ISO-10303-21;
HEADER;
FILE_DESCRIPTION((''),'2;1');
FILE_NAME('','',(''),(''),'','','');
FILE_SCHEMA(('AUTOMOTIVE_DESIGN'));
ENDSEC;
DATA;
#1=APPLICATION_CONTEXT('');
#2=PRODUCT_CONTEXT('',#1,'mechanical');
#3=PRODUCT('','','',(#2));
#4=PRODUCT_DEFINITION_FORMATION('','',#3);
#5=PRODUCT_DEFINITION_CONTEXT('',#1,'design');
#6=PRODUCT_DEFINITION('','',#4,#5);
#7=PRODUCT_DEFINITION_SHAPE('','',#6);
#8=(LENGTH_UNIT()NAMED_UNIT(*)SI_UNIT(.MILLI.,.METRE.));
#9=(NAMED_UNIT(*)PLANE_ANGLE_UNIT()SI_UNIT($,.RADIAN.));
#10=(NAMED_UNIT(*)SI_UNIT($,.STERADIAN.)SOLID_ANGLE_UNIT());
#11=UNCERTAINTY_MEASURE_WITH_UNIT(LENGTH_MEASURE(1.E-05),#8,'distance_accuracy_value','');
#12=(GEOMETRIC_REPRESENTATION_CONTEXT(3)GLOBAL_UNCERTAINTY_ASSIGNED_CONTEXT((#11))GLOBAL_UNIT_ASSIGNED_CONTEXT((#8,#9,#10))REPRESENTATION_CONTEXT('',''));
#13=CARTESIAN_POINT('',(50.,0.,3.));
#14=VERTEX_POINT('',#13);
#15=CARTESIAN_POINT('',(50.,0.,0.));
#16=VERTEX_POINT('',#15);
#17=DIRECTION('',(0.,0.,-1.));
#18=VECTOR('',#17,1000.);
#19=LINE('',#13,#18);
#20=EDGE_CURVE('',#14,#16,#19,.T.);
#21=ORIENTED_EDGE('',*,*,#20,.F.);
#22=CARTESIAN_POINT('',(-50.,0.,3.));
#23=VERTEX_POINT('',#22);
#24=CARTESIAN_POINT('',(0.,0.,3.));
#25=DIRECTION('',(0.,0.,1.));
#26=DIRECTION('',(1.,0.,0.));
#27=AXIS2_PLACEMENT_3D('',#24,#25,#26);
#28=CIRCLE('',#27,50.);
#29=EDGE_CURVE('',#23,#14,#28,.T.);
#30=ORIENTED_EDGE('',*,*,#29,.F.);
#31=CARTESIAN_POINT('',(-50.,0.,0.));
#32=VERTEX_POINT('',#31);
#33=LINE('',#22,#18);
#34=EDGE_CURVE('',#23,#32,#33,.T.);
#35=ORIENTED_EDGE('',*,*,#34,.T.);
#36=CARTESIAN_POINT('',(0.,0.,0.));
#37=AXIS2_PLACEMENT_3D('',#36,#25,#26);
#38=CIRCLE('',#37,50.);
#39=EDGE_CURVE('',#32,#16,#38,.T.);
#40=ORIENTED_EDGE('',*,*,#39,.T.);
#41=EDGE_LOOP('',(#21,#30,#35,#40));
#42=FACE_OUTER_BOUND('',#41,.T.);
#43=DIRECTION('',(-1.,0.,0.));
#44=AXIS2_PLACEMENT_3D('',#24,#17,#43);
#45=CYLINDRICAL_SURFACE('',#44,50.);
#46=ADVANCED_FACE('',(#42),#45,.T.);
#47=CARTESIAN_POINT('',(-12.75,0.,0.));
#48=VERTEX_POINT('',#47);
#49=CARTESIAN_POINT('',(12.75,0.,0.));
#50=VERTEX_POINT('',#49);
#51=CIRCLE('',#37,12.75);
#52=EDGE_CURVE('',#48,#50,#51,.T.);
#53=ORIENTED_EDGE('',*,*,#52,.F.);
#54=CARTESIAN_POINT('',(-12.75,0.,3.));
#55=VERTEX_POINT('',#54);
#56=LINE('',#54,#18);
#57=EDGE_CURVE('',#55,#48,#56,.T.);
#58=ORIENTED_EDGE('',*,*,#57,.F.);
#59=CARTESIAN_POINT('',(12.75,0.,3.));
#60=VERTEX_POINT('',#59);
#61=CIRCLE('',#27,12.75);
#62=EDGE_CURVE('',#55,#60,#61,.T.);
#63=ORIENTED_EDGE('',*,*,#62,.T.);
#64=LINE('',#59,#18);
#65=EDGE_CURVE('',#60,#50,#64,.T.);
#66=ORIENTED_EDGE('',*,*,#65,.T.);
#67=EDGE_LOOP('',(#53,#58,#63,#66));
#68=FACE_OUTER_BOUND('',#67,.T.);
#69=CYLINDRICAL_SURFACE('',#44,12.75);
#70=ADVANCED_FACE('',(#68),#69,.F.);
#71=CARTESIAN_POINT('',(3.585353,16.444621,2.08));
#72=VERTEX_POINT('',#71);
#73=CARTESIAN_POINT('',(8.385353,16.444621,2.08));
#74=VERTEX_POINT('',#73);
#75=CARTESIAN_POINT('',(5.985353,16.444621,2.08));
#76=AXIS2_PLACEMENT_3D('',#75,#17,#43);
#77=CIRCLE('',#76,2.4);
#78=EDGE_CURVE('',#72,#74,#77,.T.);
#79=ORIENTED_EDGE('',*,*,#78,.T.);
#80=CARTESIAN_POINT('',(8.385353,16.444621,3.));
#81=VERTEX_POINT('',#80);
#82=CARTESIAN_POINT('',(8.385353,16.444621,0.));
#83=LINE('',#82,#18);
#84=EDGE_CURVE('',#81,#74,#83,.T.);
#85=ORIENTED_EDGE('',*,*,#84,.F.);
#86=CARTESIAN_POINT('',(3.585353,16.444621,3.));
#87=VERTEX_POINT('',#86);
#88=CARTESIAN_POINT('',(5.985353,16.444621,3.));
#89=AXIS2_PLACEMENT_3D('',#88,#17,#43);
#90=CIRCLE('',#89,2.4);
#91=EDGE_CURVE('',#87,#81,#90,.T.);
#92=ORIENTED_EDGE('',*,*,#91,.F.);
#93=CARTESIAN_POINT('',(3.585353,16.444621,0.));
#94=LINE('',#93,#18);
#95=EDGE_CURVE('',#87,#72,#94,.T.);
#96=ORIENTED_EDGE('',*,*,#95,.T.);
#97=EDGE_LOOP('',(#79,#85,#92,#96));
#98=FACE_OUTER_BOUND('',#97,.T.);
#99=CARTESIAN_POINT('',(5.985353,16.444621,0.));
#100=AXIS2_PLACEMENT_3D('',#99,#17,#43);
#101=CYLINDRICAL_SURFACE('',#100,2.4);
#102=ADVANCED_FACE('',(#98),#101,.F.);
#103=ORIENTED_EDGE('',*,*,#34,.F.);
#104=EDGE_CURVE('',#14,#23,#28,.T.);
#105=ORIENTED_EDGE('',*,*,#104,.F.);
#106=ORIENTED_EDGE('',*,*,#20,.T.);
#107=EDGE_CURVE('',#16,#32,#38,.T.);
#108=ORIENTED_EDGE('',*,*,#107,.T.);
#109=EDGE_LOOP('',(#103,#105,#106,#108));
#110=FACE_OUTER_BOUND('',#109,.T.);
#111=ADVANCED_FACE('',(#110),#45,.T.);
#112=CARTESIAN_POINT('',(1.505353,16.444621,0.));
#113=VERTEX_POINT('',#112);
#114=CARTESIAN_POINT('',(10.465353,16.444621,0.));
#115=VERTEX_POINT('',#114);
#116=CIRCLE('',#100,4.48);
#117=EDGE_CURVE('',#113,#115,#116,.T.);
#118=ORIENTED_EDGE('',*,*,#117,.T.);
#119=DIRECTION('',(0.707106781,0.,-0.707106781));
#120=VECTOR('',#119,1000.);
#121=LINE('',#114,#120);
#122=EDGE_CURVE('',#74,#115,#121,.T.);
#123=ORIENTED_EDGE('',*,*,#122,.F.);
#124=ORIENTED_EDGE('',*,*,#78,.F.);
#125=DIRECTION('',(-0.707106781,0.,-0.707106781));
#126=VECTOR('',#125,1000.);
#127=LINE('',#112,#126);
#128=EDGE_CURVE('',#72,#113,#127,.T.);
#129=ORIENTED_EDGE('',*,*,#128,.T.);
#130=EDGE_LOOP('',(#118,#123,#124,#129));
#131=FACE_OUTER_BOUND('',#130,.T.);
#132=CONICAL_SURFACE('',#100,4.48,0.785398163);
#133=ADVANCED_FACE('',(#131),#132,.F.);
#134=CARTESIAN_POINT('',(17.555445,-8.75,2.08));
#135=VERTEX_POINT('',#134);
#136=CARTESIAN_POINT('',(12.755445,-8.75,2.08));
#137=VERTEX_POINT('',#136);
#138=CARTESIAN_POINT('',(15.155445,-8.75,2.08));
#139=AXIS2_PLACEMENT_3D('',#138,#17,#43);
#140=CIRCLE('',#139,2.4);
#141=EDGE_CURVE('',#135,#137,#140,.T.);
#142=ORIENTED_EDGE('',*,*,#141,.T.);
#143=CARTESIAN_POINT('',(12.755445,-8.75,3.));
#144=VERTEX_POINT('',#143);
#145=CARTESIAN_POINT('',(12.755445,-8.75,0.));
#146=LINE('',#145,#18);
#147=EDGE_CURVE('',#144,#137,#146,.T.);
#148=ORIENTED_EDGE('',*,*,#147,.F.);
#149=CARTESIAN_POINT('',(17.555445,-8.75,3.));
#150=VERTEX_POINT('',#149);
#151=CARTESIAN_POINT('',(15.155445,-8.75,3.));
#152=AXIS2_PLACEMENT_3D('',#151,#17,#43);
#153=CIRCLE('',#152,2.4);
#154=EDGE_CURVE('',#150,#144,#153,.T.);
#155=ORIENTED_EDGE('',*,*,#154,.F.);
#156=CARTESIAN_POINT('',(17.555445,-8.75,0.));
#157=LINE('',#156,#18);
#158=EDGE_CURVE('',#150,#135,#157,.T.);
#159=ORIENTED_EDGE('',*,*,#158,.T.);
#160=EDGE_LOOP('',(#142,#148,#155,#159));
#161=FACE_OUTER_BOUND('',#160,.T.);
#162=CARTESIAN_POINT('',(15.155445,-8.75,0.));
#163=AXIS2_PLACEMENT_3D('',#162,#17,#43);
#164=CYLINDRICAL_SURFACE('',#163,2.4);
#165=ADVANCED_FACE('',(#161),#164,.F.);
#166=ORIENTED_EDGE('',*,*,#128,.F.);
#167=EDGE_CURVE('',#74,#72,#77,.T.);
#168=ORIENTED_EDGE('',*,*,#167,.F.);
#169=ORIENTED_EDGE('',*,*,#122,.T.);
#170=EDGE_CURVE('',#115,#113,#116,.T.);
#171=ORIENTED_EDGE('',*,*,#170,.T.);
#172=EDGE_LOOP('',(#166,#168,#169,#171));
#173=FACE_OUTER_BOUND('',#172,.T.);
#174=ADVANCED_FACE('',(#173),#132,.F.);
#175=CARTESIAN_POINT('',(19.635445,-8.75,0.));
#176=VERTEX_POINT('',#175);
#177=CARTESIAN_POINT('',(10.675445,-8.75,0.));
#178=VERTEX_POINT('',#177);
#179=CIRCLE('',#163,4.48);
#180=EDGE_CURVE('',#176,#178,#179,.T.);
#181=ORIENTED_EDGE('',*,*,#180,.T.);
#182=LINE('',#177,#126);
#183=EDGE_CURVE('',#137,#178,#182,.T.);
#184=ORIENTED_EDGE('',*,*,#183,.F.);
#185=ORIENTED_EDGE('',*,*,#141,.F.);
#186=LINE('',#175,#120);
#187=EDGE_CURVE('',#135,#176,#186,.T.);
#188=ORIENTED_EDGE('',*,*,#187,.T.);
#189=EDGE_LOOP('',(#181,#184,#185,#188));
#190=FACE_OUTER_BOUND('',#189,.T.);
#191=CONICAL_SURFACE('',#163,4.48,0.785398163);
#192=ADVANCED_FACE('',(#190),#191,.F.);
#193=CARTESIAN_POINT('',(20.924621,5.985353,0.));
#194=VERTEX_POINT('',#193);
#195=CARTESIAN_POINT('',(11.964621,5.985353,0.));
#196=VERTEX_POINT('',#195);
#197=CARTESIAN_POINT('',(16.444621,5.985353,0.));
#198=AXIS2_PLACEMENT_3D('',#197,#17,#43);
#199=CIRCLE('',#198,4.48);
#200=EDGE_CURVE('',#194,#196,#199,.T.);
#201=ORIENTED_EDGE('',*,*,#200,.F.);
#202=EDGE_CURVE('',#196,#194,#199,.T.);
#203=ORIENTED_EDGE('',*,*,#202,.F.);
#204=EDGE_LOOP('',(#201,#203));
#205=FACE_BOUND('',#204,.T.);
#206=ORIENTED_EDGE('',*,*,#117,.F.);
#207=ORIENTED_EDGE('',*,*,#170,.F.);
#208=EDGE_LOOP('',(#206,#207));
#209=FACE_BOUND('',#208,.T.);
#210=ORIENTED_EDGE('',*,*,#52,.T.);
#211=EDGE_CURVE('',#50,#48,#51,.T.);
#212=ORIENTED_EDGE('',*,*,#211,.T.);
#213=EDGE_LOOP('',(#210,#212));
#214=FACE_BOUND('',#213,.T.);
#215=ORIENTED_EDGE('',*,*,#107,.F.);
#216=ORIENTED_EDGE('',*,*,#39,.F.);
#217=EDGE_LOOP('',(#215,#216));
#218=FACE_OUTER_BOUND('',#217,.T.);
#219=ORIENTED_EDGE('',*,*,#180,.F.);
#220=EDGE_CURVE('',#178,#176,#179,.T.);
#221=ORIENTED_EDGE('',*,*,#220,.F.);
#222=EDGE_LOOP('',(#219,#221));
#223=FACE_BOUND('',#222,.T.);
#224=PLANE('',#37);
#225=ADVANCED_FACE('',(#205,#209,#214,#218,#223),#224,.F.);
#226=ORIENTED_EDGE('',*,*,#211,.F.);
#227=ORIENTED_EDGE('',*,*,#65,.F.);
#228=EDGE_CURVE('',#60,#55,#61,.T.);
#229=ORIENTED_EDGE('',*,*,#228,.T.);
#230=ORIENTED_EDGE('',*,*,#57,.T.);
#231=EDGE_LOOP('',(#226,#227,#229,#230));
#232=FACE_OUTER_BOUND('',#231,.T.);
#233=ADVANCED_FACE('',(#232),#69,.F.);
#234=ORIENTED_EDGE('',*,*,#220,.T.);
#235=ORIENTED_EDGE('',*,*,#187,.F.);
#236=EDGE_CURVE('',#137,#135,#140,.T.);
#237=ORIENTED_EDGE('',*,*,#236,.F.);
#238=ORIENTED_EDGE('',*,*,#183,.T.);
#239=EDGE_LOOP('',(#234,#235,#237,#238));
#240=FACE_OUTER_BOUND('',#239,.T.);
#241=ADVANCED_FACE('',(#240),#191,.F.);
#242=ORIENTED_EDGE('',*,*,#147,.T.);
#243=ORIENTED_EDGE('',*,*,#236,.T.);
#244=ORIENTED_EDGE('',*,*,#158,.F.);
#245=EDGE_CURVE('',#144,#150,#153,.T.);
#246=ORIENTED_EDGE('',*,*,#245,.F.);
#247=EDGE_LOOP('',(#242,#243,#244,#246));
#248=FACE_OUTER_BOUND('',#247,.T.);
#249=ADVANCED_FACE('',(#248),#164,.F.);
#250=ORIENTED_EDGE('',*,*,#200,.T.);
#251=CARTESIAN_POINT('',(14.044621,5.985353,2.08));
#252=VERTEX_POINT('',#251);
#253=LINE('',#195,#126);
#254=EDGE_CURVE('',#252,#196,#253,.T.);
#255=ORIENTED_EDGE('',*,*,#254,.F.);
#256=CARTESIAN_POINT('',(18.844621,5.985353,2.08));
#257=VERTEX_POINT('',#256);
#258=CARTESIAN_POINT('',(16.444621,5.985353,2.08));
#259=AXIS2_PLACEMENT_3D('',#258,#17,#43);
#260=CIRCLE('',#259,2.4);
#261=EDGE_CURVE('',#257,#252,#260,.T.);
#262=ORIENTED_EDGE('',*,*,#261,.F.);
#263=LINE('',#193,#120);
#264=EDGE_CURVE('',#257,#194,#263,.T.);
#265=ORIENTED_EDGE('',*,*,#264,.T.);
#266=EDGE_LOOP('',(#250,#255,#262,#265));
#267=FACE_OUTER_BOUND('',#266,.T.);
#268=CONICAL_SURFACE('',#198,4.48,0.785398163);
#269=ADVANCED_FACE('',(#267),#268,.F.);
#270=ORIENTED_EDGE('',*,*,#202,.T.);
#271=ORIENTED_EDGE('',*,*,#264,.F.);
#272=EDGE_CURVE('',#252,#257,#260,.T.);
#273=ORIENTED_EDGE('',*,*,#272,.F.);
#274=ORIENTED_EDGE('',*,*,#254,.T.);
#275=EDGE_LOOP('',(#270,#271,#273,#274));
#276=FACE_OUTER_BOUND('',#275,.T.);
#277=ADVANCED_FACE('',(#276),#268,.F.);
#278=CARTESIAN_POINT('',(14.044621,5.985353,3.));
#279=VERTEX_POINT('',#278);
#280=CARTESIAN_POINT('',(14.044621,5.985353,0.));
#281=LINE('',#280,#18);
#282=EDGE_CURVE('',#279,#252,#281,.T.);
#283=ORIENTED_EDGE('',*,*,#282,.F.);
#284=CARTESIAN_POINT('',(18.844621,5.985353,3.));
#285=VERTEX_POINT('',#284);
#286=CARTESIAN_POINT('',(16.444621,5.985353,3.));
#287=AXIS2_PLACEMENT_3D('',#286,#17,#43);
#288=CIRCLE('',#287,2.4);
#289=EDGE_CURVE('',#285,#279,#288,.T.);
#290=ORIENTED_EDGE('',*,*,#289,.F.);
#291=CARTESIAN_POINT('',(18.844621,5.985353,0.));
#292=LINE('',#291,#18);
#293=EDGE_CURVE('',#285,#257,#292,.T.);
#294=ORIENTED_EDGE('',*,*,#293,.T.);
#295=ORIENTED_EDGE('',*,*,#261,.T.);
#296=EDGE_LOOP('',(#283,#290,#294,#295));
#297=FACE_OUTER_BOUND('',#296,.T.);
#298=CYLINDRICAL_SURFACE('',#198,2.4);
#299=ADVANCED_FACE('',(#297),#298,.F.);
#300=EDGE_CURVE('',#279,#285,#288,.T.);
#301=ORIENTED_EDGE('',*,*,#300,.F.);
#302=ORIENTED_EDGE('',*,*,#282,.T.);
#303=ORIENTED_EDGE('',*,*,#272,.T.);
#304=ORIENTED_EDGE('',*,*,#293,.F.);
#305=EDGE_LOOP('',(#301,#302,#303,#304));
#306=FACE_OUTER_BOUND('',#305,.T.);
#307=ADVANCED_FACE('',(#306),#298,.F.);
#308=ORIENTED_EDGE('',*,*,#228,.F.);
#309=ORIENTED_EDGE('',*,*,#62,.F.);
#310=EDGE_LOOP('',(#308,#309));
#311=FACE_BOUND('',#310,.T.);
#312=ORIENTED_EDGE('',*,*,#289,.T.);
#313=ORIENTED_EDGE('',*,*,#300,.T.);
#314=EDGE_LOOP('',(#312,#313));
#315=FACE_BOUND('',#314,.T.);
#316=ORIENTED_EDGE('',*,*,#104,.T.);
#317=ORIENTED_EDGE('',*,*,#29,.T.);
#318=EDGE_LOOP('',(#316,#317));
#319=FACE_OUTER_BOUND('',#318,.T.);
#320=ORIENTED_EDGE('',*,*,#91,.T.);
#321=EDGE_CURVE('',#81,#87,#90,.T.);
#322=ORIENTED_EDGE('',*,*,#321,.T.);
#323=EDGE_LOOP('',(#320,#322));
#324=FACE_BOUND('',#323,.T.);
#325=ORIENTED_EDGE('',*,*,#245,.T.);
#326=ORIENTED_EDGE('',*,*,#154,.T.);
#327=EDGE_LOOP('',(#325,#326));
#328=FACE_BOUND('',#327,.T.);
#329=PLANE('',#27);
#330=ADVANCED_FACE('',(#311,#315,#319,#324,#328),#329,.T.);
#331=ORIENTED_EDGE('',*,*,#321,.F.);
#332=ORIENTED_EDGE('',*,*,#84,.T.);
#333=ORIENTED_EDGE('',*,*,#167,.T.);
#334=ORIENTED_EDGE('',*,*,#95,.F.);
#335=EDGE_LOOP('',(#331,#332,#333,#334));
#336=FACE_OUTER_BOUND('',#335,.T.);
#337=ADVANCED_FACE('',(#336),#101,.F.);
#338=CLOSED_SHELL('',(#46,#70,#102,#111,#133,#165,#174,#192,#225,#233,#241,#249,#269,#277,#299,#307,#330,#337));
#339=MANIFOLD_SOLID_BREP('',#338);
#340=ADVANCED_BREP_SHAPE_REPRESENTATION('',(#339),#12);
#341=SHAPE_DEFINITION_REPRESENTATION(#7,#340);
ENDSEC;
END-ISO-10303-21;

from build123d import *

# Parameters (mm, degrees)
SKETCH1_R                                    = 50
SKETCH1_R_2                                  = 12.75
BOSS_EXTRUDE1_DEPTH                          = 3
CSK_FOR_M4_HEX_SOCKET_COUNTERSUNK_CA_2_COUNT = 2
CSK_FOR_M4_HEX_SOCKET_COUNTERSUNK_CA_2_PITCH = 26.811555509
CSK_FOR_M4_HEX_SOCKET_COUNTERSUNK_CA_3_COUNT = 2
CSK_FOR_M4_HEX_SOCKET_COUNTERSUNK_CA_3_PITCH = 14.791639161


with BuildPart() as part:
    # Sketch1 → Boss-Extrude1 (new body)
    with BuildSketch(Plane.XY):
        Circle(SKETCH1_R)
        Circle(SKETCH1_R_2, mode=Mode.SUBTRACT)
    extrude(amount=BOSS_EXTRUDE1_DEPTH)

    # Sketch2 → CSK for M4 Hex Socket Countersunk Cap Screw1 (revolve, cut)
    with BuildSketch(Plane(origin=(5.985352508, 16.444620864, 0), x_dir=(0, 1, 0), z_dir=(1, 0, 0))):
        Polygon((0, 0), (0, 3), (2.4, 3), (2.4, 2.08), (4.48, 0), align=None)
    csk_for_m4_hex_socket_countersunk_cap_sc = revolve(axis=Axis((5.985352508, 16.444620864, -6.35), (0, 0, 1)), mode=Mode.SUBTRACT)

    # CSK for M4 Hex Socket Countersunk Ca 2: CSK for M4 Hex Socket Countersunk Cap Screw1 ×2
    with Locations(*[Vector(0.3420201433256698, -0.9396926207859081, 0) * (i * CSK_FOR_M4_HEX_SOCKET_COUNTERSUNK_CA_2_PITCH) for i in range(1, CSK_FOR_M4_HEX_SOCKET_COUNTERSUNK_CA_2_COUNT)]):
        add(csk_for_m4_hex_socket_countersunk_cap_sc, mode=Mode.SUBTRACT)

    # CSK for M4 Hex Socket Countersunk Ca 3: CSK for M4 Hex Socket Countersunk Cap Screw1 ×2
    with Locations(*[Vector(0.7071067811865491, -0.707106781186546, 0) * (i * CSK_FOR_M4_HEX_SOCKET_COUNTERSUNK_CA_3_PITCH) for i in range(1, CSK_FOR_M4_HEX_SOCKET_COUNTERSUNK_CA_3_COUNT)]):
        add(csk_for_m4_hex_socket_countersunk_cap_sc, mode=Mode.SUBTRACT)


solid = part.part
